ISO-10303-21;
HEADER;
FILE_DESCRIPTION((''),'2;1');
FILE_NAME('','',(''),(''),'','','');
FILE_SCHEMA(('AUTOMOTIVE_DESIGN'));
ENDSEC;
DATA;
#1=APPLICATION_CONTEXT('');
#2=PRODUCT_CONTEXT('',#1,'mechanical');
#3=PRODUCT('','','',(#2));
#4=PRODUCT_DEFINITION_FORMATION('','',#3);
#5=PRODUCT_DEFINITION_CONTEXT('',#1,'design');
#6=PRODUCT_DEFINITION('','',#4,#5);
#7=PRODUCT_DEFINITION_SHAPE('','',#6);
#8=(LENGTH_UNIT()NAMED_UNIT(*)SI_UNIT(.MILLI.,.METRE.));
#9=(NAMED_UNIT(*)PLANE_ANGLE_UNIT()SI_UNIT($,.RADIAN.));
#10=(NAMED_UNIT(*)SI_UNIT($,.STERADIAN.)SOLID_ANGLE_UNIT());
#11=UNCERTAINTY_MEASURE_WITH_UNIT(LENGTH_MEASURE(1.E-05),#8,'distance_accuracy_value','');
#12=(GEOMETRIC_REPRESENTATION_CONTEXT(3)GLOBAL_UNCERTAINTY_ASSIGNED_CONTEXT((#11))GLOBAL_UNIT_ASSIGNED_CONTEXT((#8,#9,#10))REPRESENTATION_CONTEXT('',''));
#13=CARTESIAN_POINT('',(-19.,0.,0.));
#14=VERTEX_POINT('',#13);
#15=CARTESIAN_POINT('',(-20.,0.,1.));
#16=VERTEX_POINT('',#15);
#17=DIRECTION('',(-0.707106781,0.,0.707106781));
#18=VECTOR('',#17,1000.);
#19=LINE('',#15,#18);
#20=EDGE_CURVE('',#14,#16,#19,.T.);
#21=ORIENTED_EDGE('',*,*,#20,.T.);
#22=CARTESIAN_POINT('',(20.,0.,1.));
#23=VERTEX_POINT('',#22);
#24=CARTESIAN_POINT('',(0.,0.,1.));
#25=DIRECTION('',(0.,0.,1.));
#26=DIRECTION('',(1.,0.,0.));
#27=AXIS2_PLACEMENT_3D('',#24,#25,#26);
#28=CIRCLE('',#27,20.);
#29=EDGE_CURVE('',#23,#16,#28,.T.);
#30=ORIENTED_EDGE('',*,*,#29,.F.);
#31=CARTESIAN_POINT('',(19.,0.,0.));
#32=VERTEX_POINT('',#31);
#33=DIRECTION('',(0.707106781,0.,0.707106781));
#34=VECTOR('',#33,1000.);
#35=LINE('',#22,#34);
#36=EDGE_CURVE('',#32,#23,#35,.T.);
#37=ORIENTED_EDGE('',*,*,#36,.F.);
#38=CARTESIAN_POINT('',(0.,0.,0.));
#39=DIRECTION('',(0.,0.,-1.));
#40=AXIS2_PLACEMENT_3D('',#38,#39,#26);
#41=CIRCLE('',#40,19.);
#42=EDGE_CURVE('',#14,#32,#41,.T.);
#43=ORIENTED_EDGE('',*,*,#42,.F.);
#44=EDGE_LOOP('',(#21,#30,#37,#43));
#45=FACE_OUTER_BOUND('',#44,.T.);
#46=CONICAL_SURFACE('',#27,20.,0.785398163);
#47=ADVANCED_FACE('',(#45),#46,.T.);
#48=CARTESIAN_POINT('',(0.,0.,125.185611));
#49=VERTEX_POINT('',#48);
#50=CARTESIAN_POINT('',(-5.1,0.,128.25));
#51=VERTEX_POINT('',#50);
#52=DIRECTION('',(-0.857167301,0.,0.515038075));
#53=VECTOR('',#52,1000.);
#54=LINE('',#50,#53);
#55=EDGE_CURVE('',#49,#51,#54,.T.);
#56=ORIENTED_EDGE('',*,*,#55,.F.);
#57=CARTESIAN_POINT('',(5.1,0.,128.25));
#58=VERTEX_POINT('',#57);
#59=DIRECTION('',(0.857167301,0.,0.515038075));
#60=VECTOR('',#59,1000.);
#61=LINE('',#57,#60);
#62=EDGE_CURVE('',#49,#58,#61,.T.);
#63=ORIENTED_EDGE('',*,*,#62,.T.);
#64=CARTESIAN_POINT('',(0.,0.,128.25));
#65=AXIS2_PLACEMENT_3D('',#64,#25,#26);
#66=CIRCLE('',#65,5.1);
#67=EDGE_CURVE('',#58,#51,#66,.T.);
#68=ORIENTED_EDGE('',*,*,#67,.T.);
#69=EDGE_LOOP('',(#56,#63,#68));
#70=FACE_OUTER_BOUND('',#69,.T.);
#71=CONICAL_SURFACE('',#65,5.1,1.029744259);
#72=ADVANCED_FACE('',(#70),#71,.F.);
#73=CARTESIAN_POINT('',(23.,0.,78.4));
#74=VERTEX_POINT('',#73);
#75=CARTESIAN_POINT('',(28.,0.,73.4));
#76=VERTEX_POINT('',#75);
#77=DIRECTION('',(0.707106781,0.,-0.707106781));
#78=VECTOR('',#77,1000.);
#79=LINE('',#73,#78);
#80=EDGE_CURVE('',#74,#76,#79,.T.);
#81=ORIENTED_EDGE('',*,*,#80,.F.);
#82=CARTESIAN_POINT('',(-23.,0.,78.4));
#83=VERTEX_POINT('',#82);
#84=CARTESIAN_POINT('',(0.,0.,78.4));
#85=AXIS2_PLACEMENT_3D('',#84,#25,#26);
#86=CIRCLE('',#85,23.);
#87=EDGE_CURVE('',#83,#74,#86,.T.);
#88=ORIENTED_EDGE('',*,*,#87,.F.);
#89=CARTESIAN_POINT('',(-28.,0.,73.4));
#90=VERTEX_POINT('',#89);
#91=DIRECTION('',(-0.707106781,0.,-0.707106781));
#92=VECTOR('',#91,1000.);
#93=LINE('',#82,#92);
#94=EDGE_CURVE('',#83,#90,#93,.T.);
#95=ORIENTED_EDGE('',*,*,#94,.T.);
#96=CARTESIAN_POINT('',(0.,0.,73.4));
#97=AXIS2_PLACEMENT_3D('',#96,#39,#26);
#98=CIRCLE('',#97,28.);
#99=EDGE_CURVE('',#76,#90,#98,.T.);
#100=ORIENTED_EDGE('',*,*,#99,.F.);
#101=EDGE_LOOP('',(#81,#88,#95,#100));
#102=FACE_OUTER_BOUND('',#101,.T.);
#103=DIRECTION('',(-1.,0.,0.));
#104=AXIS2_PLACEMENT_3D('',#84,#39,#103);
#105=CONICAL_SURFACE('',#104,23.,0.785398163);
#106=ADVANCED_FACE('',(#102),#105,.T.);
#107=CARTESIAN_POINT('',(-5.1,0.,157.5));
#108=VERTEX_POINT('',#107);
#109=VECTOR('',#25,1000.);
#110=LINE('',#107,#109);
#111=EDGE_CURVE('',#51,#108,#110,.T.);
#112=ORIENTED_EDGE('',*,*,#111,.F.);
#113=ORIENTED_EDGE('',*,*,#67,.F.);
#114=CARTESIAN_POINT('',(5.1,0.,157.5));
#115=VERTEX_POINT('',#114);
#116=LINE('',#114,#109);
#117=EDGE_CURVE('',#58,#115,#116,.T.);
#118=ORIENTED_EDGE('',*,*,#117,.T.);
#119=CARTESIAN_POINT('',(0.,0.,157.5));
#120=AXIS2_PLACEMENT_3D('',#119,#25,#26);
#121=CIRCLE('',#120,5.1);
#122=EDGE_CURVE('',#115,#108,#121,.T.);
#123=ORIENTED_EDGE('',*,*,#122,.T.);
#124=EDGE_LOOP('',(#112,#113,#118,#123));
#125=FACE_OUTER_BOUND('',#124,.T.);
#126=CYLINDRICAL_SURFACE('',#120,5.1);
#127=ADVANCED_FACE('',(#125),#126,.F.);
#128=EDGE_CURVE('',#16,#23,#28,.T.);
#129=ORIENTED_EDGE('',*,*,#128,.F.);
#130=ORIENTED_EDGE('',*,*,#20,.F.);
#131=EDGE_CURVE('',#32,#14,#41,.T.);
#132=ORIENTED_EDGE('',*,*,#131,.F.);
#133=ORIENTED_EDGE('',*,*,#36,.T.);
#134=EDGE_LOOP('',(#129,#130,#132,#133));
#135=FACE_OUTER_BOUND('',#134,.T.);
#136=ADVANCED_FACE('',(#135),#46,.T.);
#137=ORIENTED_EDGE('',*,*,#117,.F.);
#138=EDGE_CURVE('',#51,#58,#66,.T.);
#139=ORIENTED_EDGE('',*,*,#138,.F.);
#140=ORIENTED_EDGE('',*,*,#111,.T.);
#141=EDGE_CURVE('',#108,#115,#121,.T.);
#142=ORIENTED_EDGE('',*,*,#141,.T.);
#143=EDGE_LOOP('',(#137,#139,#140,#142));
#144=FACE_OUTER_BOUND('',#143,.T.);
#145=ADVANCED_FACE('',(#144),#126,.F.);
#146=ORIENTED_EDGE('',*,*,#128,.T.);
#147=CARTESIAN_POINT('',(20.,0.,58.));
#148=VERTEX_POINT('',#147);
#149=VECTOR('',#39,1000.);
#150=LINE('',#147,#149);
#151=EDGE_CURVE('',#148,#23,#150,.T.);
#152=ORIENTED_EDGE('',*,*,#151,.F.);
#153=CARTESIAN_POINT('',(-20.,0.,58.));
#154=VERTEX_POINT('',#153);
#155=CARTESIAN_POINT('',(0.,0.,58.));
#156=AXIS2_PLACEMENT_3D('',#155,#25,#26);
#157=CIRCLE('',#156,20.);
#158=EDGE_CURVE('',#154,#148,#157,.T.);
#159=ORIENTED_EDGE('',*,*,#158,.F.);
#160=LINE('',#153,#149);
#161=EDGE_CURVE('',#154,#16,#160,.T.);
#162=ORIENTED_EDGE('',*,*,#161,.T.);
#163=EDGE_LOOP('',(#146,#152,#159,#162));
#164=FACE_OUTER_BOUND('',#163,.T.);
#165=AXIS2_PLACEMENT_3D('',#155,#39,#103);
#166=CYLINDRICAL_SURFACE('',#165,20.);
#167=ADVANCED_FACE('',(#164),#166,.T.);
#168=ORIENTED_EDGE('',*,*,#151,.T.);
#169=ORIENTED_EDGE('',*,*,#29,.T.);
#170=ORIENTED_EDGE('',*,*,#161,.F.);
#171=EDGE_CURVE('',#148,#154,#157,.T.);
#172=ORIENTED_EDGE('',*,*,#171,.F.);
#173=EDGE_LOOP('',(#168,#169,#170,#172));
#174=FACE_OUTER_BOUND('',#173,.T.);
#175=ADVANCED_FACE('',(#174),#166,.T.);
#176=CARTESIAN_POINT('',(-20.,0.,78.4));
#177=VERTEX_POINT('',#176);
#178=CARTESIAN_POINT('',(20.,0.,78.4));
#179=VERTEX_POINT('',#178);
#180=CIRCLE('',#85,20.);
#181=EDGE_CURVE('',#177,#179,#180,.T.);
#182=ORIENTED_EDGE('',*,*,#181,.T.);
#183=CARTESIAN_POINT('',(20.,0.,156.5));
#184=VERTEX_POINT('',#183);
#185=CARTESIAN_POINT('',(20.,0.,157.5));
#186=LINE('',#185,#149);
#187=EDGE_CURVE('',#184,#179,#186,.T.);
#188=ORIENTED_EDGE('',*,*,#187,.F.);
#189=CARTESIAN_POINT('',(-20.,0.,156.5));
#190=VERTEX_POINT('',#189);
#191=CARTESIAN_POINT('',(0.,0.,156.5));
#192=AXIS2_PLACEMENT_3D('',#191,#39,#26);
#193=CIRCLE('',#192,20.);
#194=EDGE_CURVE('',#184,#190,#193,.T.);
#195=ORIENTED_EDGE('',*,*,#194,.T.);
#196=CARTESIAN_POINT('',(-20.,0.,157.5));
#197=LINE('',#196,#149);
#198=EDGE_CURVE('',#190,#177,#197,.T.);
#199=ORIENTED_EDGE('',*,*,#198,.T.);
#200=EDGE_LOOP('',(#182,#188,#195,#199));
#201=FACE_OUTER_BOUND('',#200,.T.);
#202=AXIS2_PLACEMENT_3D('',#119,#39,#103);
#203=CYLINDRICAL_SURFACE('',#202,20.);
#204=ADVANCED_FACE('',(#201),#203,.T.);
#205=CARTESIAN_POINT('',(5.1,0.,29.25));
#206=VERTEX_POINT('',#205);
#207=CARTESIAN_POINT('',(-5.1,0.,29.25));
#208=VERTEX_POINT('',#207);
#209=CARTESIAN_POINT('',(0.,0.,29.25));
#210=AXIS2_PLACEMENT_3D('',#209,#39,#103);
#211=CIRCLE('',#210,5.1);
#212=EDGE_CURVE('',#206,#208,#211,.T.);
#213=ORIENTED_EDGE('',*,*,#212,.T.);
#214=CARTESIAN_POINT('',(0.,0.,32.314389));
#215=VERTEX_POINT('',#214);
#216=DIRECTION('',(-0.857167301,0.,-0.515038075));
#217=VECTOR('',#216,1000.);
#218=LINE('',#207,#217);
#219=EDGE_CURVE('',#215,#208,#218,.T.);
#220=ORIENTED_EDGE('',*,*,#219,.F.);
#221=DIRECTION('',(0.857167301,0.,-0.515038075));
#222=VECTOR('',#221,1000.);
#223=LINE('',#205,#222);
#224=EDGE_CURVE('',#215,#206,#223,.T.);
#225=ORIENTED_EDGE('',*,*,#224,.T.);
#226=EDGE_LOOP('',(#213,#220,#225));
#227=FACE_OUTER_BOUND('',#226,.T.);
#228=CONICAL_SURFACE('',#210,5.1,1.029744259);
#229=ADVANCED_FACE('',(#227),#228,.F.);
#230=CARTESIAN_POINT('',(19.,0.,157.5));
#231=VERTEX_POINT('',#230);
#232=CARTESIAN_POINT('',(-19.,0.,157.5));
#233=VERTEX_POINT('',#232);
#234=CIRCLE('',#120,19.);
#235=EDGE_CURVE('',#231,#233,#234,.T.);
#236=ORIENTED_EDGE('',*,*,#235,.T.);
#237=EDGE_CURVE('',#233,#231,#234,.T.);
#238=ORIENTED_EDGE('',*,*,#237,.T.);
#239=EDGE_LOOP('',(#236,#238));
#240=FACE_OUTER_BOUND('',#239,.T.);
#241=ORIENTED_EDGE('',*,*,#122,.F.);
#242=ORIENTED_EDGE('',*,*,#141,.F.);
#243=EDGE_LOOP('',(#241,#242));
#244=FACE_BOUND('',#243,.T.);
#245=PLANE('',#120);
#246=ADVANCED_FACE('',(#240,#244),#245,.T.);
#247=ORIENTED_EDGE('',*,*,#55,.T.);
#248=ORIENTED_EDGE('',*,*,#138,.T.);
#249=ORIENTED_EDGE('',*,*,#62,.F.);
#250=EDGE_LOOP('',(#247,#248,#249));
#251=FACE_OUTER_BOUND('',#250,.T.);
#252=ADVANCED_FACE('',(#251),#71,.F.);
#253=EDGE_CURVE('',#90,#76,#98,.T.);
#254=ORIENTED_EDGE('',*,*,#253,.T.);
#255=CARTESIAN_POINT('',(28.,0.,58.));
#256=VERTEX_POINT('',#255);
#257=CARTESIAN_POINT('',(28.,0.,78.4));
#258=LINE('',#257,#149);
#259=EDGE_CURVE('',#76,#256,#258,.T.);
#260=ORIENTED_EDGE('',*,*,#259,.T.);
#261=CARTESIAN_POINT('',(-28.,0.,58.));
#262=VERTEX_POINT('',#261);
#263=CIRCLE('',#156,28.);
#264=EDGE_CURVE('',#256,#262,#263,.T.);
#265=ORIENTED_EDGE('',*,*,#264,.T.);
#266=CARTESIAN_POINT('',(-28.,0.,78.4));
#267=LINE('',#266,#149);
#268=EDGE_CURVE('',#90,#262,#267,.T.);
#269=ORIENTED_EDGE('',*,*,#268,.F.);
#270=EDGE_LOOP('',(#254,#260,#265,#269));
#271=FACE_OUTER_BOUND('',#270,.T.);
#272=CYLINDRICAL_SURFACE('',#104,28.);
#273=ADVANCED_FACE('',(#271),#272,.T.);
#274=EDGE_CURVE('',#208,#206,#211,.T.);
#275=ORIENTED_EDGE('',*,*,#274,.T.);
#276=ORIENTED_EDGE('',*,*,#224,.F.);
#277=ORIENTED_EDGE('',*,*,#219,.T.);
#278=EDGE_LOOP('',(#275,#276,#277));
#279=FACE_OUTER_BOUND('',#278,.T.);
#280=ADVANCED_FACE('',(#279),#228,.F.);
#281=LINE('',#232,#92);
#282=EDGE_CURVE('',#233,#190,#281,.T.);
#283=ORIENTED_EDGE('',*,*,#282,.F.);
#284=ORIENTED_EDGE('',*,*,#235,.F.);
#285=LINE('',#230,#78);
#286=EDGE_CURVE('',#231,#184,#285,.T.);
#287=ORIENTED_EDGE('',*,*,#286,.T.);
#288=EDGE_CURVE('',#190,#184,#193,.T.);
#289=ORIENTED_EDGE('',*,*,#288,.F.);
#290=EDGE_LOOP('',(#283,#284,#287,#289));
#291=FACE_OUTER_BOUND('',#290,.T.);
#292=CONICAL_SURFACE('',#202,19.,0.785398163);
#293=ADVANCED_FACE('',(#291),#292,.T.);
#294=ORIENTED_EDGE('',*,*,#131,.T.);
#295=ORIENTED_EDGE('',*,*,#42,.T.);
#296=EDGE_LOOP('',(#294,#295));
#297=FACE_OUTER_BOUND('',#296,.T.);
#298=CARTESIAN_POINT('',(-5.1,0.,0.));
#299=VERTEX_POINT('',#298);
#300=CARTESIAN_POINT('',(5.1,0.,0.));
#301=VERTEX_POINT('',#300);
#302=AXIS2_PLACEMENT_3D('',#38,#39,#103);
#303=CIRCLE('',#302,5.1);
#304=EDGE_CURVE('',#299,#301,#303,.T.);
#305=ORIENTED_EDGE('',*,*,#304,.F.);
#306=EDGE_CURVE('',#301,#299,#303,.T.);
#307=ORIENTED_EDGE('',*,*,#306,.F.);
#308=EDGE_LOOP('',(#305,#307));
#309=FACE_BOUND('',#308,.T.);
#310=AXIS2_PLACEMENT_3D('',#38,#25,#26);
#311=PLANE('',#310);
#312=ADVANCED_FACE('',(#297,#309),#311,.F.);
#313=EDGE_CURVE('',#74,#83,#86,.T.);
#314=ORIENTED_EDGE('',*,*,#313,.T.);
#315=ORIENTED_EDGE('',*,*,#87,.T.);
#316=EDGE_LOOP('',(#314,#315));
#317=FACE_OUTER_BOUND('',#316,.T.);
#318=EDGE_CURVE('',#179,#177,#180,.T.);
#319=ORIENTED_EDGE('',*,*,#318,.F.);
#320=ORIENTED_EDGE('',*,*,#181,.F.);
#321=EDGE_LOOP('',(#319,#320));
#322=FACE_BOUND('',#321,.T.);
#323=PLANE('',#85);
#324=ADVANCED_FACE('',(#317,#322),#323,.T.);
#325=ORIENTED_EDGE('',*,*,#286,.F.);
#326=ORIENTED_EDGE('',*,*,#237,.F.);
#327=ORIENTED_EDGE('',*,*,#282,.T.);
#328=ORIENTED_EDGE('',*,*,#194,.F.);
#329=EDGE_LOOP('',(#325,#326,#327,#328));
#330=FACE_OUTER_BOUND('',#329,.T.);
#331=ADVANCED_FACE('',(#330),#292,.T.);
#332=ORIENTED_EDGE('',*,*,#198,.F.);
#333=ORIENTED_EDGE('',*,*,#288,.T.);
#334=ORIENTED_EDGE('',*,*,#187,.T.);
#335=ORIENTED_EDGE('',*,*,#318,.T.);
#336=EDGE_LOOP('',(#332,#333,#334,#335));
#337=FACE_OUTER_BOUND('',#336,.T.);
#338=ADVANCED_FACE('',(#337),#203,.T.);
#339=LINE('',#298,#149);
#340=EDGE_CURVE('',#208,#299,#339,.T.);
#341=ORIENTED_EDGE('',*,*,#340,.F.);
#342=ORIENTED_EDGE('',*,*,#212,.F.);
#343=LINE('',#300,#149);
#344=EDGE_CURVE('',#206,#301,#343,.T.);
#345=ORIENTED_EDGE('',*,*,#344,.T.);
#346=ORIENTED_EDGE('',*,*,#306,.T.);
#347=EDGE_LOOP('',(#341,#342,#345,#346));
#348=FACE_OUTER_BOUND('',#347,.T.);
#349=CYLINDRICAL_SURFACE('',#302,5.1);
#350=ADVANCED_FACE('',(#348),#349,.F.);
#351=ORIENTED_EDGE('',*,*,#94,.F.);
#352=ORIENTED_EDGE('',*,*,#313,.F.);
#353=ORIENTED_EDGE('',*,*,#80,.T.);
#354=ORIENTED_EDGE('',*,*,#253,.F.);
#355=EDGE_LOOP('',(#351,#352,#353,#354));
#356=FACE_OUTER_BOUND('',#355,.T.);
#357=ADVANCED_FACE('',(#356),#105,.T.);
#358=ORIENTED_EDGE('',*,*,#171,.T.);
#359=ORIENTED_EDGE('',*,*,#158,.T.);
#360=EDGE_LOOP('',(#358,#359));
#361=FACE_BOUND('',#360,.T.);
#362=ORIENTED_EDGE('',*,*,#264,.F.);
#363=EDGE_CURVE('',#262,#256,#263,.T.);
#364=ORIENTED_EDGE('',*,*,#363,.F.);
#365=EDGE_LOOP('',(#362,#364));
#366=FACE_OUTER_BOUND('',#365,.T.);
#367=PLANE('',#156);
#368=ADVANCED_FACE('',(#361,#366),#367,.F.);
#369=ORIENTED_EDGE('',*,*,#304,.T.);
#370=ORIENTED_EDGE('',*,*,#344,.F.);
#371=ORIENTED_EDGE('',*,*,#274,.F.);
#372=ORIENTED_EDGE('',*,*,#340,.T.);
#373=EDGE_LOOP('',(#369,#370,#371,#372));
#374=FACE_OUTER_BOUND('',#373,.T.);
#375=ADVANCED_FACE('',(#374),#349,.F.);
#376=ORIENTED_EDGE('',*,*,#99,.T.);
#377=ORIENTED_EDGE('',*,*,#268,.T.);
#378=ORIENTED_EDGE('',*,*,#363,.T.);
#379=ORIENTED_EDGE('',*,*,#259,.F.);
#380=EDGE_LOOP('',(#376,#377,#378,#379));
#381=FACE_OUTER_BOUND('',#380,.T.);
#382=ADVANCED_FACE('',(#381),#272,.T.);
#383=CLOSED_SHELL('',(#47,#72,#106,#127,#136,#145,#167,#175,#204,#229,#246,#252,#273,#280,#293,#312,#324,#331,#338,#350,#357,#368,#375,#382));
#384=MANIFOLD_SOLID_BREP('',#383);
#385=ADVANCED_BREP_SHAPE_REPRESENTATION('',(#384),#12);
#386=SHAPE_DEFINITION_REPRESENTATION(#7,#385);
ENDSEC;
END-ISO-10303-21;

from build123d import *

# Parameters (mm, degrees)
SKETCH_1_R              = 20
EXTRUDE_1_DEPTH         = 58
SKETCH_2_R              = 28
EXTRUDE_2_DEPTH         = 20.4
SKETCH_3_R              = 20
EXTRUDE_3_DEPTH         = 79.1
CHAMFER_1_SIZE          = 5
CHAMFER_2_SIZE          = 1
HOLE_WIZARD_M12_1_D     = 10.2
HOLE_WIZARD_M12_1_DEPTH = 29.25
HOLE_WIZARD_M12_1_TIP   = 3.064389157
HOLE_WIZARD_M12_2_D     = 10.2
HOLE_WIZARD_M12_2_DEPTH = 29.25
HOLE_WIZARD_M12_2_TIP   = 3.064389157


with BuildPart() as part:
    # 草图1 → 凸台-拉伸1 (new body)
    with BuildSketch(Plane.XY):
        with Locations(Location((0, 0, 0), (0, 0, 180))):
            Circle(SKETCH_1_R)
    extrude(amount=EXTRUDE_1_DEPTH)

    # 草图2 → 凸台-拉伸2 (add)
    with BuildSketch(Plane.XY.offset(58)):
        Circle(SKETCH_2_R)
    extrude(amount=EXTRUDE_2_DEPTH)

    # 草图3 → 凸台-拉伸3 (add)
    with BuildSketch(Plane.XY.offset(78.4)):
        with Locations(Location((0, 0, 0), (0, 0, 180))):
            Circle(SKETCH_3_R)
    extrude(amount=EXTRUDE_3_DEPTH)

    # 倒角1
    chamfer_1_edges = [part.edges().sort_by_distance(p)[0] for p in [
        (-28, 0, 78.4),
    ]]
    chamfer(chamfer_1_edges, length=CHAMFER_1_SIZE)

    # 倒角2
    chamfer_2_edges = [part.edges().sort_by_distance(p)[0] for p in [
        (20, 0, 157.5),
        (20, 0, 0),
    ]]
    chamfer(chamfer_2_edges, length=CHAMFER_2_SIZE)

    # M12 螺纹孔1
    with Locations(Plane(origin=(0, 0, 0), x_dir=(-1, 0, 0), z_dir=(0, 0, -1))):
        with Locations((0, 0)):
            Hole(HOLE_WIZARD_M12_1_D / 2, depth=HOLE_WIZARD_M12_1_DEPTH)
            with Locations((0, 0, -(HOLE_WIZARD_M12_1_DEPTH + HOLE_WIZARD_M12_1_TIP / 2))):  # 118° drill point
                Cone(0, HOLE_WIZARD_M12_1_D / 2, HOLE_WIZARD_M12_1_TIP, mode=Mode.SUBTRACT)

    # M12 螺纹孔2
    with Locations(Plane.XY.offset(157.5)):
        with Locations((0, 0)):
            Hole(HOLE_WIZARD_M12_2_D / 2, depth=HOLE_WIZARD_M12_2_DEPTH)
            with Locations((0, 0, -(HOLE_WIZARD_M12_2_DEPTH + HOLE_WIZARD_M12_2_TIP / 2))):  # 118° drill point
                Cone(0, HOLE_WIZARD_M12_2_D / 2, HOLE_WIZARD_M12_2_TIP, mode=Mode.SUBTRACT)


solid = part.part
